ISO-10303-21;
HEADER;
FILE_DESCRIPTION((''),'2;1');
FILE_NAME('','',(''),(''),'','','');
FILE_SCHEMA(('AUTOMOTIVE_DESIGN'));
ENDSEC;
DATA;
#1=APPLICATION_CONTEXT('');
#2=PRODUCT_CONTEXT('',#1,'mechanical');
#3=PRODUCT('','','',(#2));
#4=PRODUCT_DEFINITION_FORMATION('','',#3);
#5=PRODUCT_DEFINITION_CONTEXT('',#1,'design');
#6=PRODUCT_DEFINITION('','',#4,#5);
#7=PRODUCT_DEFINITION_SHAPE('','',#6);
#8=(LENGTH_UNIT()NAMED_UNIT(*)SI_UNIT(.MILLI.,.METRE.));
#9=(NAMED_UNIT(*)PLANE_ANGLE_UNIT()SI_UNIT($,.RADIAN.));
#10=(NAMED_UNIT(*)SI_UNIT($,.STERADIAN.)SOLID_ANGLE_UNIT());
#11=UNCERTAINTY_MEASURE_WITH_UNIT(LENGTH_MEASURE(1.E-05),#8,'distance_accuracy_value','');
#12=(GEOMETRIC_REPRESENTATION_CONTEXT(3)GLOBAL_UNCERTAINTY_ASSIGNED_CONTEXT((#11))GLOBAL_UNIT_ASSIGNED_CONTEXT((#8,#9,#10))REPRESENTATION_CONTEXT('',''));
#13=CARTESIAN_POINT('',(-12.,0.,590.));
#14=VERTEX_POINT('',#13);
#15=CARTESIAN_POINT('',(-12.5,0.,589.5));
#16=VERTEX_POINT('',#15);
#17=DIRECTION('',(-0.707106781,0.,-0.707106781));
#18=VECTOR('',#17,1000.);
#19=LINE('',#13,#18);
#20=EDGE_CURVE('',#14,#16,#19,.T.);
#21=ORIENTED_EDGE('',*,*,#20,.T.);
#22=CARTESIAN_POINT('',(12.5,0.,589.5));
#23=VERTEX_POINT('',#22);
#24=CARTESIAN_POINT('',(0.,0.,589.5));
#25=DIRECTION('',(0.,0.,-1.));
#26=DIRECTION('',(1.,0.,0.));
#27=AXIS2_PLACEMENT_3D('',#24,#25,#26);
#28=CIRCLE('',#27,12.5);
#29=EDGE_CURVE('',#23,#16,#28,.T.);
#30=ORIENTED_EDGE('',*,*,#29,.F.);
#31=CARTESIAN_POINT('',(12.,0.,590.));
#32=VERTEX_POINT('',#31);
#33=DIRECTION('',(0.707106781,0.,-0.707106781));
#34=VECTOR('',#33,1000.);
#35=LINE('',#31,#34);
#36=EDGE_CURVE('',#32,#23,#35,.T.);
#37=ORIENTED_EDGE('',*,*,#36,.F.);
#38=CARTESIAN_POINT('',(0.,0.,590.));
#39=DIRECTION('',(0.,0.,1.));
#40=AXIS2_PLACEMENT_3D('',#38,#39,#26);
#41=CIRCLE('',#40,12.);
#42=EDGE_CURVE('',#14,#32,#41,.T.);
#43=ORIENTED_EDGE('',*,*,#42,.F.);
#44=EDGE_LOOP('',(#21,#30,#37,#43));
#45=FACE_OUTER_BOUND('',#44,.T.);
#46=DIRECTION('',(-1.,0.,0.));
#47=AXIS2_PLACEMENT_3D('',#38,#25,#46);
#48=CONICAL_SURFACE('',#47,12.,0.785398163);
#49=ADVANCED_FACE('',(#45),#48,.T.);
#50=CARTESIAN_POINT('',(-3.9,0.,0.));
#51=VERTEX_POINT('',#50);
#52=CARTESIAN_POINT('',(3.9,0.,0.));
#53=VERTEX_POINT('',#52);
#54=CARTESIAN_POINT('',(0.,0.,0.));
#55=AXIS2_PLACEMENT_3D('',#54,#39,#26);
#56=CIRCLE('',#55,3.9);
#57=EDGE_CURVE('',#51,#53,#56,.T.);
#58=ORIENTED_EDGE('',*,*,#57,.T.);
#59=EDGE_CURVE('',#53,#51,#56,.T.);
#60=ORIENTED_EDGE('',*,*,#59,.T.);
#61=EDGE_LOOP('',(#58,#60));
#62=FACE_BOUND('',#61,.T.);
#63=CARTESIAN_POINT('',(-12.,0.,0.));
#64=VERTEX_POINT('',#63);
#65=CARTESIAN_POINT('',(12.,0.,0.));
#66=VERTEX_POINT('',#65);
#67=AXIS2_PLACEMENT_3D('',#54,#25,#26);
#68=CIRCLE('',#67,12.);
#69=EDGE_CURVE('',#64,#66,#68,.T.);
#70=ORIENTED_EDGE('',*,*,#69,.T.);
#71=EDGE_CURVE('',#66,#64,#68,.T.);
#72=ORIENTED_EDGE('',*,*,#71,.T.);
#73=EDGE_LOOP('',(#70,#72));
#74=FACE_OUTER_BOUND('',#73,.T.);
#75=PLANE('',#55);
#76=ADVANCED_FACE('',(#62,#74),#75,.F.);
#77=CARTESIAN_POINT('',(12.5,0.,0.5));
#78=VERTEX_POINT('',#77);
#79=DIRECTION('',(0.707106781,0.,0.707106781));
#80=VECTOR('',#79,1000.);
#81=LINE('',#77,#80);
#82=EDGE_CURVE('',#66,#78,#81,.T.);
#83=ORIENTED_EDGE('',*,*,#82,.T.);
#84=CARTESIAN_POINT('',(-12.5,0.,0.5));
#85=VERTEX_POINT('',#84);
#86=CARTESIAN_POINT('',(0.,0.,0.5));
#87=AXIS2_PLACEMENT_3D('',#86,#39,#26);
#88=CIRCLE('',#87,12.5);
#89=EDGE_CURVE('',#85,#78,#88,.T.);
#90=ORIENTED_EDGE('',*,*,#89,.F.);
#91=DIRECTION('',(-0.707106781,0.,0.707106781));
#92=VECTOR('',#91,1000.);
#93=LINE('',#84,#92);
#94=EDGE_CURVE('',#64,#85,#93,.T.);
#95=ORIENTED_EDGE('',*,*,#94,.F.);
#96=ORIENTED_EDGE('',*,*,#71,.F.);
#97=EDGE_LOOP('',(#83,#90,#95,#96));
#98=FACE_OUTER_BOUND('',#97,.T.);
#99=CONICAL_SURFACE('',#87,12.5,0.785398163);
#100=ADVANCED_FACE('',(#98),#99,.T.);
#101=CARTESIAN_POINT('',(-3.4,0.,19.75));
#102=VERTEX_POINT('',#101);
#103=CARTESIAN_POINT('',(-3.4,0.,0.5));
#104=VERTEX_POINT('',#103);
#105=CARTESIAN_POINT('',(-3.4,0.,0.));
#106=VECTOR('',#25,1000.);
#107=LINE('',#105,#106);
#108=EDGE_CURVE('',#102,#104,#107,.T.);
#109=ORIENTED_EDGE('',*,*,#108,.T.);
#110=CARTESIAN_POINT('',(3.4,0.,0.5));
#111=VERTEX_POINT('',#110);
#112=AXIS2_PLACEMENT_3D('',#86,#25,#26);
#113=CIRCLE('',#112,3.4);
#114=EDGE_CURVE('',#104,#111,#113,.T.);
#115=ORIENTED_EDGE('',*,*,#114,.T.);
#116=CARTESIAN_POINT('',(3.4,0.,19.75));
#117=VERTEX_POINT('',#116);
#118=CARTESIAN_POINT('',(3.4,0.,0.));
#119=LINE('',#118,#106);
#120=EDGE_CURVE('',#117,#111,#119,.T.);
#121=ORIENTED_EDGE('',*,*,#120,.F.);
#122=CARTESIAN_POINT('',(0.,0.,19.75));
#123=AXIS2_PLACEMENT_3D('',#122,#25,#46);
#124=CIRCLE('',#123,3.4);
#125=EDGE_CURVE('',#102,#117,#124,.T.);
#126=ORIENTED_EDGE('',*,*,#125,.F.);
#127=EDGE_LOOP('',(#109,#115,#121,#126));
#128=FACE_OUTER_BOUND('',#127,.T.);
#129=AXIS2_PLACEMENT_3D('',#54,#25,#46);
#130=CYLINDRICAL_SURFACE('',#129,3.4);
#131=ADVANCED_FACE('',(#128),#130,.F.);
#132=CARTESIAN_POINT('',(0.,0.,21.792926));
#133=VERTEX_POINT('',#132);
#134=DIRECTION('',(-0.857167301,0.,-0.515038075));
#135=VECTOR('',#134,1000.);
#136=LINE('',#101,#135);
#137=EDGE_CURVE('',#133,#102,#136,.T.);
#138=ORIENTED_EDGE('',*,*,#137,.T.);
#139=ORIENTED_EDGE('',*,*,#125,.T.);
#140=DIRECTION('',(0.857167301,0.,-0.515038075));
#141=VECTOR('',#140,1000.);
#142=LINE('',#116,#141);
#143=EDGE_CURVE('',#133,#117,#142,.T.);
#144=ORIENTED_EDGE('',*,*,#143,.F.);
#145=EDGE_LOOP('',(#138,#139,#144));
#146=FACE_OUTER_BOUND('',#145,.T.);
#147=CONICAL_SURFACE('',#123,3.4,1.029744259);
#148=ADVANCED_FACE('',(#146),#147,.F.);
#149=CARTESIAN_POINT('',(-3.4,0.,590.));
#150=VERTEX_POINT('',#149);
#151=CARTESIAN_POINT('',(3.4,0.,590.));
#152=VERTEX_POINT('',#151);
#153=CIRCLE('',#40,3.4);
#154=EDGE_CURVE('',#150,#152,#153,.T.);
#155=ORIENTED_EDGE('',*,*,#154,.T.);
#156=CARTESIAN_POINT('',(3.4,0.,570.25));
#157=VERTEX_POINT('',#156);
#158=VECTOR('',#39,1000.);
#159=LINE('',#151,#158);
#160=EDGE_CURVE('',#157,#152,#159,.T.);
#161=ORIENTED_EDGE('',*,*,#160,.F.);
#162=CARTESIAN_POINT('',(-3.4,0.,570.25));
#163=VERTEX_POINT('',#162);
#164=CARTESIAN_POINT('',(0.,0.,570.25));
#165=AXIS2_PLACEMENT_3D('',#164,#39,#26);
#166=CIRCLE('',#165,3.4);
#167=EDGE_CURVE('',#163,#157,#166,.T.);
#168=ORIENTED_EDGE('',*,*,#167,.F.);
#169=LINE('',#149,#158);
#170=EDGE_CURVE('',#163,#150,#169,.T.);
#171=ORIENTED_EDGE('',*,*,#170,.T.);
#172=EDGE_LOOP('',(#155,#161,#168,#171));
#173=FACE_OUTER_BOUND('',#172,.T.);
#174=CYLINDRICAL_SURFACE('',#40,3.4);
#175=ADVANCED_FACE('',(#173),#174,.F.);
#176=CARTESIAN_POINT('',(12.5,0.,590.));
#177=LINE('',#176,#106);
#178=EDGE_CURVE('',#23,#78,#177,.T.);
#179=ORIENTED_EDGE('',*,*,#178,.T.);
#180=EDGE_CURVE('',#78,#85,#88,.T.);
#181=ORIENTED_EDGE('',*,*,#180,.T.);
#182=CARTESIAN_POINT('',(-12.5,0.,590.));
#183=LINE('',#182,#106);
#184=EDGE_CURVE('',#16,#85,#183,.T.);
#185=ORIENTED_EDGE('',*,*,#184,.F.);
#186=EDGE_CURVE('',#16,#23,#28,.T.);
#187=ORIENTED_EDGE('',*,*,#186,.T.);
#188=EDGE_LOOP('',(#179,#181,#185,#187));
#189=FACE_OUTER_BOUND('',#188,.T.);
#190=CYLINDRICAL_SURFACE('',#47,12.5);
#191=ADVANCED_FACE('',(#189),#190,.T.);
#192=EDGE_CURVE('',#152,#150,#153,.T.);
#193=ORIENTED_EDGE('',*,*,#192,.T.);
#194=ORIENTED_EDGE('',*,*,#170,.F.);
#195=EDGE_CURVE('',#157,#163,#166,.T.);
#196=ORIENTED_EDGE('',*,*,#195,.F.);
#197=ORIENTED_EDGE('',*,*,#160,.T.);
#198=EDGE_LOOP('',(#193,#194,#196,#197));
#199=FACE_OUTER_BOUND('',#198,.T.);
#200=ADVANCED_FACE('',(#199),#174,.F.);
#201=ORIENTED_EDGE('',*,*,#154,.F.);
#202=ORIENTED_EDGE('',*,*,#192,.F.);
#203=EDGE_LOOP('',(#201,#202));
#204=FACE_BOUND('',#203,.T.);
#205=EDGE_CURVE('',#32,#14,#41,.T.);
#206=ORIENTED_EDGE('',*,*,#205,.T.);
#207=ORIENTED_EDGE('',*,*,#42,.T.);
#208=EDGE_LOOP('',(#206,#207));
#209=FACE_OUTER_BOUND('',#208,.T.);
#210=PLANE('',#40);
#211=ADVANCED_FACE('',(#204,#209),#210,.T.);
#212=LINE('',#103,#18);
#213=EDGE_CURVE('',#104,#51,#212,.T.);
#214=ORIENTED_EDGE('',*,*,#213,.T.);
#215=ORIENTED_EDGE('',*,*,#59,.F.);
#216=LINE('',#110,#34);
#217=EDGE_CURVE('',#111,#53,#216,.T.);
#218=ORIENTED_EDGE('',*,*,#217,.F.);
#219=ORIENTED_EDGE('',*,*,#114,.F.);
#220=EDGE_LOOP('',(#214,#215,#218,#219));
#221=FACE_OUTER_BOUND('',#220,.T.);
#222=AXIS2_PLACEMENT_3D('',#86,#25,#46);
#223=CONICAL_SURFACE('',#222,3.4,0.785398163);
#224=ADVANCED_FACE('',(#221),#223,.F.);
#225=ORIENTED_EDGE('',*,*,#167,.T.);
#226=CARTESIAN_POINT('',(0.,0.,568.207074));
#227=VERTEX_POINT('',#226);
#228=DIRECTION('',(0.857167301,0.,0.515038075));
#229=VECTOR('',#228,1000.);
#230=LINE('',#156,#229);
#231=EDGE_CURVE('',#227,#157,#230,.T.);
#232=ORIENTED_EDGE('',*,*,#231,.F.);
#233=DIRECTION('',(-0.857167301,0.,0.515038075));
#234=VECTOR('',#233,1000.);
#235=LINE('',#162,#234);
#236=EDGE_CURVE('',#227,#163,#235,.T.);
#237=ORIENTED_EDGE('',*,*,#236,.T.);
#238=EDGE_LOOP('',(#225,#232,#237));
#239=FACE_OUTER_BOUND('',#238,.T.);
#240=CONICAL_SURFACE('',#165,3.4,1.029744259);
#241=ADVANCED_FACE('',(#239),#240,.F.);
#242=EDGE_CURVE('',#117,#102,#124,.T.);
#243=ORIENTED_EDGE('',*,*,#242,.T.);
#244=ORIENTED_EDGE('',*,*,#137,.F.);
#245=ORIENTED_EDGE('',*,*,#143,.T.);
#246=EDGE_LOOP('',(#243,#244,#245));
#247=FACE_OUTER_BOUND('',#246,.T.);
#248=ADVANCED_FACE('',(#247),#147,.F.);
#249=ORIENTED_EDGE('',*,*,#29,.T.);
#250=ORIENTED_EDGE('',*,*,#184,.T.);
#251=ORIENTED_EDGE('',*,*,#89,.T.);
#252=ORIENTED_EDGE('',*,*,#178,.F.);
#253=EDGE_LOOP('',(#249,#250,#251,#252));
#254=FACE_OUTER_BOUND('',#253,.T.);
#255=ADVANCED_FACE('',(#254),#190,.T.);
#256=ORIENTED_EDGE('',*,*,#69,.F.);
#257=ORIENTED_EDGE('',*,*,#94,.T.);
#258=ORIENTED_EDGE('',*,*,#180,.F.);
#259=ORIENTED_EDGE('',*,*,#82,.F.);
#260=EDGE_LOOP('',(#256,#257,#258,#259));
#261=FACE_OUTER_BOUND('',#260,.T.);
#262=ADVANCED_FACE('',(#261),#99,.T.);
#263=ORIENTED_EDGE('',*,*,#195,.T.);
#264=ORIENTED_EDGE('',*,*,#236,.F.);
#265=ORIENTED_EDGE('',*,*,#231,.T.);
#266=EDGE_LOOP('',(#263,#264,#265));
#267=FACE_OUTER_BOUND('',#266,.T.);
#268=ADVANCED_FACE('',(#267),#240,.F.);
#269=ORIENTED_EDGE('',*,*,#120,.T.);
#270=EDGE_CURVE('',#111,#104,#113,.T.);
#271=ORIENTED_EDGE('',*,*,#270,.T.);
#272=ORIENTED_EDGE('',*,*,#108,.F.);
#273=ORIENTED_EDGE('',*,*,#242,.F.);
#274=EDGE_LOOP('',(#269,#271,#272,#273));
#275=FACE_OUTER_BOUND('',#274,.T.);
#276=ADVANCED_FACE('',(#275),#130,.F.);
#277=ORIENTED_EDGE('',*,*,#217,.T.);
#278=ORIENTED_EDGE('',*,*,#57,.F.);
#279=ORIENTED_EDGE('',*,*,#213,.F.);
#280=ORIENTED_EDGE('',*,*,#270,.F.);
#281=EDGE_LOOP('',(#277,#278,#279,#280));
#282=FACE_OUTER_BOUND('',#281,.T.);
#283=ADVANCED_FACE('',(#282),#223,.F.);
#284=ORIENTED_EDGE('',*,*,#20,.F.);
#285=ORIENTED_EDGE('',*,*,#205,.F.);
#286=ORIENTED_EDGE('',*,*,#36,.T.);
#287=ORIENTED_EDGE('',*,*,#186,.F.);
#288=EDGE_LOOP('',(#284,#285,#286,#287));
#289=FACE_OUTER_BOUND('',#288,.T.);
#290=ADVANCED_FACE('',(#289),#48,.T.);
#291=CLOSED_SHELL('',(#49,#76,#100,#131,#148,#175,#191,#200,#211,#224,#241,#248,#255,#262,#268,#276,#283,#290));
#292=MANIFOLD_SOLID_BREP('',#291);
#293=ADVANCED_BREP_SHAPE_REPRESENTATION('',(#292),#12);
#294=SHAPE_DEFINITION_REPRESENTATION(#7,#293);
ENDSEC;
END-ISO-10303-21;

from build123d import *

# Parameters (mm, degrees)
SKETCH_1_R             = 12.5
EXTRUDE_1_DEPTH        = 590
HOLE_WIZARD_M8_1_D     = 6.8
HOLE_WIZARD_M8_1_DEPTH = 19.75
HOLE_WIZARD_M8_1_TIP   = 2.042926105
HOLE_WIZARD_M8_2_D     = 6.8
HOLE_WIZARD_M8_2_DEPTH = 19.75
HOLE_WIZARD_M8_2_TIP   = 2.042926105
CHAMFER_1_SIZE         = 0.5


with BuildPart() as part:
    # 草图1 → 凸台-拉伸1 (new body)
    with BuildSketch(Plane.XY):
        Circle(SKETCH_1_R)
    extrude(amount=EXTRUDE_1_DEPTH)

    # M8 螺纹孔1
    with Locations(Plane.XY.offset(590)):
        with Locations((0, 0)):
            Hole(HOLE_WIZARD_M8_1_D / 2, depth=HOLE_WIZARD_M8_1_DEPTH)
            with Locations((0, 0, -(HOLE_WIZARD_M8_1_DEPTH + HOLE_WIZARD_M8_1_TIP / 2))):  # 118° drill point
                Cone(0, HOLE_WIZARD_M8_1_D / 2, HOLE_WIZARD_M8_1_TIP, mode=Mode.SUBTRACT)

    # M8 螺纹孔2
    with Locations(Plane(origin=(0, 0, 0), x_dir=(-1, 0, 0), z_dir=(0, 0, -1))):
        with Locations((0, 0)):
            Hole(HOLE_WIZARD_M8_2_D / 2, depth=HOLE_WIZARD_M8_2_DEPTH)
            with Locations((0, 0, -(HOLE_WIZARD_M8_2_DEPTH + HOLE_WIZARD_M8_2_TIP / 2))):  # 118° drill point
                Cone(0, HOLE_WIZARD_M8_2_D / 2, HOLE_WIZARD_M8_2_TIP, mode=Mode.SUBTRACT)

    # 倒角1
    chamfer_1_edges = [part.edges().sort_by_distance(p)[0] for p in [
        (-3.4, 0, 0),
        (-12.5, 0, 0),
        (-12.5, 0, 590),
    ]]
    chamfer(chamfer_1_edges, length=CHAMFER_1_SIZE)


solid = part.part
